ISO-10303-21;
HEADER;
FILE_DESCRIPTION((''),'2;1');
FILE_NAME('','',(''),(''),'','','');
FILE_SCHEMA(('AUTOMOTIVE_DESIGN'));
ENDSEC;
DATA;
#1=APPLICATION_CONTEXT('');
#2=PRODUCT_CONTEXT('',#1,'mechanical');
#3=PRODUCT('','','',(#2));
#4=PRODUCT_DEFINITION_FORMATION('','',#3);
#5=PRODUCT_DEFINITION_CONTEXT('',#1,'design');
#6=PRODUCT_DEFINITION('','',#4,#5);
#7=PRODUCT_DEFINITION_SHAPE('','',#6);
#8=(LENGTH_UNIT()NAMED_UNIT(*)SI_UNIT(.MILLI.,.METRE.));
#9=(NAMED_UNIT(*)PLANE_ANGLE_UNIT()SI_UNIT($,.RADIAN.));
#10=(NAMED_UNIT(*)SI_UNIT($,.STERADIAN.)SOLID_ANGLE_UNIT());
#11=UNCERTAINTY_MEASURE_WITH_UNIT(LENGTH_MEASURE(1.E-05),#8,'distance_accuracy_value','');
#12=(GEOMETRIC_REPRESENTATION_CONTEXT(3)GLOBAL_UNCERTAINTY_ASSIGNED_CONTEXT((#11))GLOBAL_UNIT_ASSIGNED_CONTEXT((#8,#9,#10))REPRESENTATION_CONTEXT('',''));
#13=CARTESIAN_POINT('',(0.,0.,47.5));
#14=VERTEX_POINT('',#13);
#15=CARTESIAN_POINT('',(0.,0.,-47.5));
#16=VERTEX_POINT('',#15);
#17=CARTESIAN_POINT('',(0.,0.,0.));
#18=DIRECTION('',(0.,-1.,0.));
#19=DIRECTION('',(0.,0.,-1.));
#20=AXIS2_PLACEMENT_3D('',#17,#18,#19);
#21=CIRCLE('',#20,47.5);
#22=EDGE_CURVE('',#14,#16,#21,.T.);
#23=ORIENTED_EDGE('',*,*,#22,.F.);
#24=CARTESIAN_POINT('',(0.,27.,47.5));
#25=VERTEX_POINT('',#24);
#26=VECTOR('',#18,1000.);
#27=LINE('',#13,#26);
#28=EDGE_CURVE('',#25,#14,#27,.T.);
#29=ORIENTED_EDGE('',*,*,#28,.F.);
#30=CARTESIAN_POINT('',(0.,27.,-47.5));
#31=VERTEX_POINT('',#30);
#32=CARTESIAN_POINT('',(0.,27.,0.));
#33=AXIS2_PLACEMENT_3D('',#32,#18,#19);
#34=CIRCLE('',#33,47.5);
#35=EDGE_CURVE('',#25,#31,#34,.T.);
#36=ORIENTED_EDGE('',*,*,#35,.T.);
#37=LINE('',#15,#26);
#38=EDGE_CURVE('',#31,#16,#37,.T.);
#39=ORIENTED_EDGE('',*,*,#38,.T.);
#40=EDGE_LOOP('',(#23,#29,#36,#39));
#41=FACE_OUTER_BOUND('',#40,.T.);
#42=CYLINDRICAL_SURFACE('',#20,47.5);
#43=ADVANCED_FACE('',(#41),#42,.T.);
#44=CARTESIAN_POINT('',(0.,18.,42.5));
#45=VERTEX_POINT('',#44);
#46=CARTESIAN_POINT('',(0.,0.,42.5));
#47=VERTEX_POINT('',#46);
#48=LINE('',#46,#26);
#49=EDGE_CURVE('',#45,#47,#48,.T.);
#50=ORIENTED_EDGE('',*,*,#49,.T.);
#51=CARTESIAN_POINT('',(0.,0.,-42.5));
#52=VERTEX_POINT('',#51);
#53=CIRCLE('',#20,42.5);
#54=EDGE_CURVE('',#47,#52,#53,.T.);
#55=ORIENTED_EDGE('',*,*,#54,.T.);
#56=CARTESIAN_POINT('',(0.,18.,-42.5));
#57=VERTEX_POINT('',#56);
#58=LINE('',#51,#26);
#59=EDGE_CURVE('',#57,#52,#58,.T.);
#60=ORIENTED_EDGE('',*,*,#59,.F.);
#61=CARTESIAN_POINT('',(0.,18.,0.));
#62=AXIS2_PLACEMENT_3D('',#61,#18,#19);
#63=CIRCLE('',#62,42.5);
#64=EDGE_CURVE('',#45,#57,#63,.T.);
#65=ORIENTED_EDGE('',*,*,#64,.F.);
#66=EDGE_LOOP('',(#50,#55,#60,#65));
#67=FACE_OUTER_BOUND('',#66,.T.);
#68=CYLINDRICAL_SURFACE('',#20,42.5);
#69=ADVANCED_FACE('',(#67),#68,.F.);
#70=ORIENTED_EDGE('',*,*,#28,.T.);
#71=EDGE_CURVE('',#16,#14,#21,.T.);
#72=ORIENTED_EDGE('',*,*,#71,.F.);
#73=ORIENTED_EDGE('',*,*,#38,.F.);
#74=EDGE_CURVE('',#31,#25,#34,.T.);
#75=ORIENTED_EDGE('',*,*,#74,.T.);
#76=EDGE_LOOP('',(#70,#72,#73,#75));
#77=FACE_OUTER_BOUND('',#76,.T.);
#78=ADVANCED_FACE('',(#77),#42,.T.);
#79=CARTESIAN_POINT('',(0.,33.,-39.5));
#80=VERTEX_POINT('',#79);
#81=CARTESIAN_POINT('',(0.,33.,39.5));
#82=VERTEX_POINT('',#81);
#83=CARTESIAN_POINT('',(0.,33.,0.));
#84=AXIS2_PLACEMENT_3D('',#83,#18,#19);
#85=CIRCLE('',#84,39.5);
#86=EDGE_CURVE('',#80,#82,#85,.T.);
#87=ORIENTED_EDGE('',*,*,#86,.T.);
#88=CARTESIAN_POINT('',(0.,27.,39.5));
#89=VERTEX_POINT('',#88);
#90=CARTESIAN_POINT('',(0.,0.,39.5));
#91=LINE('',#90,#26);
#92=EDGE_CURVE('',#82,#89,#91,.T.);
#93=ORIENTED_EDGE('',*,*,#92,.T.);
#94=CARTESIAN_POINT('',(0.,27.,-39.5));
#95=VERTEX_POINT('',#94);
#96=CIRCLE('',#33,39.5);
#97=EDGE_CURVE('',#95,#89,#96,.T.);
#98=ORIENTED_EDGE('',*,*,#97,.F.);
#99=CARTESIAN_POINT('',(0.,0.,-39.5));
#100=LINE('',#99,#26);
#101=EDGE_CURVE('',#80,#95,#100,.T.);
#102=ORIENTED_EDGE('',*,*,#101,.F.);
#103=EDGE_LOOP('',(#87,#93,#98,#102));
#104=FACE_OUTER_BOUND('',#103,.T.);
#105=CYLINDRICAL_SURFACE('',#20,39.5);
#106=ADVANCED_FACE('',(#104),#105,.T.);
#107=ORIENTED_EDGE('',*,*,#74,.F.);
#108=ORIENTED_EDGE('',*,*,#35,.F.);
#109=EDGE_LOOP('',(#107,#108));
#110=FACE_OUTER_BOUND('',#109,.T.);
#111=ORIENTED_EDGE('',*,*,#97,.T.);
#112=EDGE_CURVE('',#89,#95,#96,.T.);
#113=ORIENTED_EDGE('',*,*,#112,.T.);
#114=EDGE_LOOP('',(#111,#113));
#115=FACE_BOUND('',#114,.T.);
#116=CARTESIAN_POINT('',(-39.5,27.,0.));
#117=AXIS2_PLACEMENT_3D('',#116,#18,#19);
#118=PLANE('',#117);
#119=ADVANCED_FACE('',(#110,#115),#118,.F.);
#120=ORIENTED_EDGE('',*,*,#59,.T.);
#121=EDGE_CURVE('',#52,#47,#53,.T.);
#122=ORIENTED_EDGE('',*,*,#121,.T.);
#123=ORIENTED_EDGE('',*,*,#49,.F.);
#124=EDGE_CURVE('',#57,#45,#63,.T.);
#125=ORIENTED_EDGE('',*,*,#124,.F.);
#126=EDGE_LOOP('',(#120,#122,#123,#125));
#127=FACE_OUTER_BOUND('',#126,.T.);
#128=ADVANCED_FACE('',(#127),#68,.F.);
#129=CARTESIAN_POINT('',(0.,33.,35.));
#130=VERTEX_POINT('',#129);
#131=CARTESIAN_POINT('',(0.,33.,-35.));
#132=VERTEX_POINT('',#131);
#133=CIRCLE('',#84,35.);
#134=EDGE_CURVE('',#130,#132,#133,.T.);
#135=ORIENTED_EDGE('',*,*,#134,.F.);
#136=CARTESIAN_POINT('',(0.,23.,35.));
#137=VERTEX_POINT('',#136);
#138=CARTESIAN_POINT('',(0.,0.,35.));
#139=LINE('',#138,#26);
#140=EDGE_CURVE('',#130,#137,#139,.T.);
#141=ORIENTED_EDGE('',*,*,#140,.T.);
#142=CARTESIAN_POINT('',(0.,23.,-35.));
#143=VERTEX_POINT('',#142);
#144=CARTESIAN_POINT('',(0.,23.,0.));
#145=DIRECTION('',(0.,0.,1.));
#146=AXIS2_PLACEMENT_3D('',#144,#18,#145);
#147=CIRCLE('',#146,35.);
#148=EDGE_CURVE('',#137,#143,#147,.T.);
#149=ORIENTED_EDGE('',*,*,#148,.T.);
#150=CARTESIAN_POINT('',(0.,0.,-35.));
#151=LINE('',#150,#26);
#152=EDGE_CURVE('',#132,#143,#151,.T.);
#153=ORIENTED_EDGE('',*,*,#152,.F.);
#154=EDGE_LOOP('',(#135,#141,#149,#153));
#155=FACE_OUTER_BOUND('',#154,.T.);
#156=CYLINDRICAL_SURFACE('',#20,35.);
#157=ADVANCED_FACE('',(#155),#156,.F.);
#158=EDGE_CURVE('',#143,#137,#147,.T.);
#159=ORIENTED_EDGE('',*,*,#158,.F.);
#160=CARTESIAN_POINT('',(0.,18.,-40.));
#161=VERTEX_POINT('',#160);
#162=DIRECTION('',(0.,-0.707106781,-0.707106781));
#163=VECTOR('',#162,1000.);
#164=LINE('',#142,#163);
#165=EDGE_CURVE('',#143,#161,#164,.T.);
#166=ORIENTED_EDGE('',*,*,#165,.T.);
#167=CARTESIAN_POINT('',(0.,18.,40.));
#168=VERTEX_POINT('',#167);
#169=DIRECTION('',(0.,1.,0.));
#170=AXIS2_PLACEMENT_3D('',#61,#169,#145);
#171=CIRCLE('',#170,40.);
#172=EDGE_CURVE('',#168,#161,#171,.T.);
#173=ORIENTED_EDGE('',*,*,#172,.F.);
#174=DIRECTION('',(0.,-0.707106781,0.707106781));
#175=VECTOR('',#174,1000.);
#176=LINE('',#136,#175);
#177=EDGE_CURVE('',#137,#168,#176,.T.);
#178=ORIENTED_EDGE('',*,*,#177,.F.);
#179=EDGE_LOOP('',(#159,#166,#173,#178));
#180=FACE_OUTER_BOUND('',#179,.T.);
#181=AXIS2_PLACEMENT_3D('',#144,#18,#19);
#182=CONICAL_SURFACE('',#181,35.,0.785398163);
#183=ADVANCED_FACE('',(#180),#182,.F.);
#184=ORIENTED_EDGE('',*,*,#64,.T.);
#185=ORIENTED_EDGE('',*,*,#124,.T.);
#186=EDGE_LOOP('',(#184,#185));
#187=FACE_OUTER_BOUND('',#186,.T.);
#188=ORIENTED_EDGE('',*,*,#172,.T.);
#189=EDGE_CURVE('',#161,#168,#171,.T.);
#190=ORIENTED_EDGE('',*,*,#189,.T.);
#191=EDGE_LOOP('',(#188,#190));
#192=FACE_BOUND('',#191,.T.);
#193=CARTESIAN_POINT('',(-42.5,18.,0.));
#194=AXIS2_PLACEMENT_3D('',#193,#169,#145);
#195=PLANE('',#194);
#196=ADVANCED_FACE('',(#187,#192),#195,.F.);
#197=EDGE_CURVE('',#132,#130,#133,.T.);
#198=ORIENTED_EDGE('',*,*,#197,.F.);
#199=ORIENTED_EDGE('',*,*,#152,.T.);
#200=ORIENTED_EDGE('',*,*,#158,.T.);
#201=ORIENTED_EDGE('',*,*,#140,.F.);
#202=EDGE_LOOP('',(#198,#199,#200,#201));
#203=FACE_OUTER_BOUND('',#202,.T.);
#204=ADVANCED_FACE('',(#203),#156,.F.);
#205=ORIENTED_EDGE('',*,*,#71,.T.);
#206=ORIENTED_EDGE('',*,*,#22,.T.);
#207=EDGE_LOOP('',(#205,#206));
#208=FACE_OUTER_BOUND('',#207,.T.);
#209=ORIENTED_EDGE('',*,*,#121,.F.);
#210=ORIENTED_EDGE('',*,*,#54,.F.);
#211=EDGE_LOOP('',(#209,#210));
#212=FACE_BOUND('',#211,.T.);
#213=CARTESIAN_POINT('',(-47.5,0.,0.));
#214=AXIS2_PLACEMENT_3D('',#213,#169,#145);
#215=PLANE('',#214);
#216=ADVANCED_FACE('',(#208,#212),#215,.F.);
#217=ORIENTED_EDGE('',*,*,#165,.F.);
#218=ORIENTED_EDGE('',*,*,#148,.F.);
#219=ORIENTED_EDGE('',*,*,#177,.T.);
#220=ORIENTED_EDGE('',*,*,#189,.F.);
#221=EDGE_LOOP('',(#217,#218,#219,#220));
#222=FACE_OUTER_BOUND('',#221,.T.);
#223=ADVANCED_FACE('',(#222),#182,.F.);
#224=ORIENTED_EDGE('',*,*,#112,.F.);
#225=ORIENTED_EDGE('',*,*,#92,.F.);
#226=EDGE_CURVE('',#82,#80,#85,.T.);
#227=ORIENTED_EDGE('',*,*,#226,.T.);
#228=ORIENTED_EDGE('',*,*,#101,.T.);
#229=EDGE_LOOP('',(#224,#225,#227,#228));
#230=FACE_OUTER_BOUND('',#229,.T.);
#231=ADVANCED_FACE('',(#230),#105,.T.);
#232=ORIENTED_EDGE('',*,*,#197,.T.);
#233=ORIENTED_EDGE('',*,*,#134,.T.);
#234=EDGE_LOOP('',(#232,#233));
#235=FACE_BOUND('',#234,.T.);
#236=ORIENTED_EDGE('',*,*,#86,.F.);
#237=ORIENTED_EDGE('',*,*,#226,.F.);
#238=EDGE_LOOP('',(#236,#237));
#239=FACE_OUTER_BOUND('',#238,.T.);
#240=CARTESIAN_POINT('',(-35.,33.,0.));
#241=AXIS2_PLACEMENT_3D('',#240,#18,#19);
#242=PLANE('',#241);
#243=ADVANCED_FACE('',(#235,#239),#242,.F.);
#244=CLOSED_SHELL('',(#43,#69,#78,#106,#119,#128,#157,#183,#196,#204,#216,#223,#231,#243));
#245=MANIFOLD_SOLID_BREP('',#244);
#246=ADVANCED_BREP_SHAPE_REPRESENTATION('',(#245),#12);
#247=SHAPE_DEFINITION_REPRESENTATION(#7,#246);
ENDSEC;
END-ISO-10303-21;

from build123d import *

# Parameters (mm, degrees)
CHAMFER_1_SIZE = 5


with BuildPart() as part:
    # 草图2 → 旋转1 (revolve)
    with BuildSketch(Plane.XY, mode=Mode.PRIVATE) as revolve_1_sk:
        Polygon((-35, 33), (-39.5, 33), (-39.5, 27), (-47.5, 27), (-47.5, 0), (-42.5, 0), (-42.5, 18), (-35, 18), align=None)
    revolve(revolve_1_sk.sketch.rotate(Axis((0, 0, 0), (0, 1, 0)), 270), axis=Axis((0, 0, 0), (0, 1, 0)))

    # 倒角1
    chamfer_1_edges = [part.edges().sort_by_distance(p)[0] for p in [
        (0, 18, 35),
    ]]
    chamfer(chamfer_1_edges, length=CHAMFER_1_SIZE)


solid = part.part
